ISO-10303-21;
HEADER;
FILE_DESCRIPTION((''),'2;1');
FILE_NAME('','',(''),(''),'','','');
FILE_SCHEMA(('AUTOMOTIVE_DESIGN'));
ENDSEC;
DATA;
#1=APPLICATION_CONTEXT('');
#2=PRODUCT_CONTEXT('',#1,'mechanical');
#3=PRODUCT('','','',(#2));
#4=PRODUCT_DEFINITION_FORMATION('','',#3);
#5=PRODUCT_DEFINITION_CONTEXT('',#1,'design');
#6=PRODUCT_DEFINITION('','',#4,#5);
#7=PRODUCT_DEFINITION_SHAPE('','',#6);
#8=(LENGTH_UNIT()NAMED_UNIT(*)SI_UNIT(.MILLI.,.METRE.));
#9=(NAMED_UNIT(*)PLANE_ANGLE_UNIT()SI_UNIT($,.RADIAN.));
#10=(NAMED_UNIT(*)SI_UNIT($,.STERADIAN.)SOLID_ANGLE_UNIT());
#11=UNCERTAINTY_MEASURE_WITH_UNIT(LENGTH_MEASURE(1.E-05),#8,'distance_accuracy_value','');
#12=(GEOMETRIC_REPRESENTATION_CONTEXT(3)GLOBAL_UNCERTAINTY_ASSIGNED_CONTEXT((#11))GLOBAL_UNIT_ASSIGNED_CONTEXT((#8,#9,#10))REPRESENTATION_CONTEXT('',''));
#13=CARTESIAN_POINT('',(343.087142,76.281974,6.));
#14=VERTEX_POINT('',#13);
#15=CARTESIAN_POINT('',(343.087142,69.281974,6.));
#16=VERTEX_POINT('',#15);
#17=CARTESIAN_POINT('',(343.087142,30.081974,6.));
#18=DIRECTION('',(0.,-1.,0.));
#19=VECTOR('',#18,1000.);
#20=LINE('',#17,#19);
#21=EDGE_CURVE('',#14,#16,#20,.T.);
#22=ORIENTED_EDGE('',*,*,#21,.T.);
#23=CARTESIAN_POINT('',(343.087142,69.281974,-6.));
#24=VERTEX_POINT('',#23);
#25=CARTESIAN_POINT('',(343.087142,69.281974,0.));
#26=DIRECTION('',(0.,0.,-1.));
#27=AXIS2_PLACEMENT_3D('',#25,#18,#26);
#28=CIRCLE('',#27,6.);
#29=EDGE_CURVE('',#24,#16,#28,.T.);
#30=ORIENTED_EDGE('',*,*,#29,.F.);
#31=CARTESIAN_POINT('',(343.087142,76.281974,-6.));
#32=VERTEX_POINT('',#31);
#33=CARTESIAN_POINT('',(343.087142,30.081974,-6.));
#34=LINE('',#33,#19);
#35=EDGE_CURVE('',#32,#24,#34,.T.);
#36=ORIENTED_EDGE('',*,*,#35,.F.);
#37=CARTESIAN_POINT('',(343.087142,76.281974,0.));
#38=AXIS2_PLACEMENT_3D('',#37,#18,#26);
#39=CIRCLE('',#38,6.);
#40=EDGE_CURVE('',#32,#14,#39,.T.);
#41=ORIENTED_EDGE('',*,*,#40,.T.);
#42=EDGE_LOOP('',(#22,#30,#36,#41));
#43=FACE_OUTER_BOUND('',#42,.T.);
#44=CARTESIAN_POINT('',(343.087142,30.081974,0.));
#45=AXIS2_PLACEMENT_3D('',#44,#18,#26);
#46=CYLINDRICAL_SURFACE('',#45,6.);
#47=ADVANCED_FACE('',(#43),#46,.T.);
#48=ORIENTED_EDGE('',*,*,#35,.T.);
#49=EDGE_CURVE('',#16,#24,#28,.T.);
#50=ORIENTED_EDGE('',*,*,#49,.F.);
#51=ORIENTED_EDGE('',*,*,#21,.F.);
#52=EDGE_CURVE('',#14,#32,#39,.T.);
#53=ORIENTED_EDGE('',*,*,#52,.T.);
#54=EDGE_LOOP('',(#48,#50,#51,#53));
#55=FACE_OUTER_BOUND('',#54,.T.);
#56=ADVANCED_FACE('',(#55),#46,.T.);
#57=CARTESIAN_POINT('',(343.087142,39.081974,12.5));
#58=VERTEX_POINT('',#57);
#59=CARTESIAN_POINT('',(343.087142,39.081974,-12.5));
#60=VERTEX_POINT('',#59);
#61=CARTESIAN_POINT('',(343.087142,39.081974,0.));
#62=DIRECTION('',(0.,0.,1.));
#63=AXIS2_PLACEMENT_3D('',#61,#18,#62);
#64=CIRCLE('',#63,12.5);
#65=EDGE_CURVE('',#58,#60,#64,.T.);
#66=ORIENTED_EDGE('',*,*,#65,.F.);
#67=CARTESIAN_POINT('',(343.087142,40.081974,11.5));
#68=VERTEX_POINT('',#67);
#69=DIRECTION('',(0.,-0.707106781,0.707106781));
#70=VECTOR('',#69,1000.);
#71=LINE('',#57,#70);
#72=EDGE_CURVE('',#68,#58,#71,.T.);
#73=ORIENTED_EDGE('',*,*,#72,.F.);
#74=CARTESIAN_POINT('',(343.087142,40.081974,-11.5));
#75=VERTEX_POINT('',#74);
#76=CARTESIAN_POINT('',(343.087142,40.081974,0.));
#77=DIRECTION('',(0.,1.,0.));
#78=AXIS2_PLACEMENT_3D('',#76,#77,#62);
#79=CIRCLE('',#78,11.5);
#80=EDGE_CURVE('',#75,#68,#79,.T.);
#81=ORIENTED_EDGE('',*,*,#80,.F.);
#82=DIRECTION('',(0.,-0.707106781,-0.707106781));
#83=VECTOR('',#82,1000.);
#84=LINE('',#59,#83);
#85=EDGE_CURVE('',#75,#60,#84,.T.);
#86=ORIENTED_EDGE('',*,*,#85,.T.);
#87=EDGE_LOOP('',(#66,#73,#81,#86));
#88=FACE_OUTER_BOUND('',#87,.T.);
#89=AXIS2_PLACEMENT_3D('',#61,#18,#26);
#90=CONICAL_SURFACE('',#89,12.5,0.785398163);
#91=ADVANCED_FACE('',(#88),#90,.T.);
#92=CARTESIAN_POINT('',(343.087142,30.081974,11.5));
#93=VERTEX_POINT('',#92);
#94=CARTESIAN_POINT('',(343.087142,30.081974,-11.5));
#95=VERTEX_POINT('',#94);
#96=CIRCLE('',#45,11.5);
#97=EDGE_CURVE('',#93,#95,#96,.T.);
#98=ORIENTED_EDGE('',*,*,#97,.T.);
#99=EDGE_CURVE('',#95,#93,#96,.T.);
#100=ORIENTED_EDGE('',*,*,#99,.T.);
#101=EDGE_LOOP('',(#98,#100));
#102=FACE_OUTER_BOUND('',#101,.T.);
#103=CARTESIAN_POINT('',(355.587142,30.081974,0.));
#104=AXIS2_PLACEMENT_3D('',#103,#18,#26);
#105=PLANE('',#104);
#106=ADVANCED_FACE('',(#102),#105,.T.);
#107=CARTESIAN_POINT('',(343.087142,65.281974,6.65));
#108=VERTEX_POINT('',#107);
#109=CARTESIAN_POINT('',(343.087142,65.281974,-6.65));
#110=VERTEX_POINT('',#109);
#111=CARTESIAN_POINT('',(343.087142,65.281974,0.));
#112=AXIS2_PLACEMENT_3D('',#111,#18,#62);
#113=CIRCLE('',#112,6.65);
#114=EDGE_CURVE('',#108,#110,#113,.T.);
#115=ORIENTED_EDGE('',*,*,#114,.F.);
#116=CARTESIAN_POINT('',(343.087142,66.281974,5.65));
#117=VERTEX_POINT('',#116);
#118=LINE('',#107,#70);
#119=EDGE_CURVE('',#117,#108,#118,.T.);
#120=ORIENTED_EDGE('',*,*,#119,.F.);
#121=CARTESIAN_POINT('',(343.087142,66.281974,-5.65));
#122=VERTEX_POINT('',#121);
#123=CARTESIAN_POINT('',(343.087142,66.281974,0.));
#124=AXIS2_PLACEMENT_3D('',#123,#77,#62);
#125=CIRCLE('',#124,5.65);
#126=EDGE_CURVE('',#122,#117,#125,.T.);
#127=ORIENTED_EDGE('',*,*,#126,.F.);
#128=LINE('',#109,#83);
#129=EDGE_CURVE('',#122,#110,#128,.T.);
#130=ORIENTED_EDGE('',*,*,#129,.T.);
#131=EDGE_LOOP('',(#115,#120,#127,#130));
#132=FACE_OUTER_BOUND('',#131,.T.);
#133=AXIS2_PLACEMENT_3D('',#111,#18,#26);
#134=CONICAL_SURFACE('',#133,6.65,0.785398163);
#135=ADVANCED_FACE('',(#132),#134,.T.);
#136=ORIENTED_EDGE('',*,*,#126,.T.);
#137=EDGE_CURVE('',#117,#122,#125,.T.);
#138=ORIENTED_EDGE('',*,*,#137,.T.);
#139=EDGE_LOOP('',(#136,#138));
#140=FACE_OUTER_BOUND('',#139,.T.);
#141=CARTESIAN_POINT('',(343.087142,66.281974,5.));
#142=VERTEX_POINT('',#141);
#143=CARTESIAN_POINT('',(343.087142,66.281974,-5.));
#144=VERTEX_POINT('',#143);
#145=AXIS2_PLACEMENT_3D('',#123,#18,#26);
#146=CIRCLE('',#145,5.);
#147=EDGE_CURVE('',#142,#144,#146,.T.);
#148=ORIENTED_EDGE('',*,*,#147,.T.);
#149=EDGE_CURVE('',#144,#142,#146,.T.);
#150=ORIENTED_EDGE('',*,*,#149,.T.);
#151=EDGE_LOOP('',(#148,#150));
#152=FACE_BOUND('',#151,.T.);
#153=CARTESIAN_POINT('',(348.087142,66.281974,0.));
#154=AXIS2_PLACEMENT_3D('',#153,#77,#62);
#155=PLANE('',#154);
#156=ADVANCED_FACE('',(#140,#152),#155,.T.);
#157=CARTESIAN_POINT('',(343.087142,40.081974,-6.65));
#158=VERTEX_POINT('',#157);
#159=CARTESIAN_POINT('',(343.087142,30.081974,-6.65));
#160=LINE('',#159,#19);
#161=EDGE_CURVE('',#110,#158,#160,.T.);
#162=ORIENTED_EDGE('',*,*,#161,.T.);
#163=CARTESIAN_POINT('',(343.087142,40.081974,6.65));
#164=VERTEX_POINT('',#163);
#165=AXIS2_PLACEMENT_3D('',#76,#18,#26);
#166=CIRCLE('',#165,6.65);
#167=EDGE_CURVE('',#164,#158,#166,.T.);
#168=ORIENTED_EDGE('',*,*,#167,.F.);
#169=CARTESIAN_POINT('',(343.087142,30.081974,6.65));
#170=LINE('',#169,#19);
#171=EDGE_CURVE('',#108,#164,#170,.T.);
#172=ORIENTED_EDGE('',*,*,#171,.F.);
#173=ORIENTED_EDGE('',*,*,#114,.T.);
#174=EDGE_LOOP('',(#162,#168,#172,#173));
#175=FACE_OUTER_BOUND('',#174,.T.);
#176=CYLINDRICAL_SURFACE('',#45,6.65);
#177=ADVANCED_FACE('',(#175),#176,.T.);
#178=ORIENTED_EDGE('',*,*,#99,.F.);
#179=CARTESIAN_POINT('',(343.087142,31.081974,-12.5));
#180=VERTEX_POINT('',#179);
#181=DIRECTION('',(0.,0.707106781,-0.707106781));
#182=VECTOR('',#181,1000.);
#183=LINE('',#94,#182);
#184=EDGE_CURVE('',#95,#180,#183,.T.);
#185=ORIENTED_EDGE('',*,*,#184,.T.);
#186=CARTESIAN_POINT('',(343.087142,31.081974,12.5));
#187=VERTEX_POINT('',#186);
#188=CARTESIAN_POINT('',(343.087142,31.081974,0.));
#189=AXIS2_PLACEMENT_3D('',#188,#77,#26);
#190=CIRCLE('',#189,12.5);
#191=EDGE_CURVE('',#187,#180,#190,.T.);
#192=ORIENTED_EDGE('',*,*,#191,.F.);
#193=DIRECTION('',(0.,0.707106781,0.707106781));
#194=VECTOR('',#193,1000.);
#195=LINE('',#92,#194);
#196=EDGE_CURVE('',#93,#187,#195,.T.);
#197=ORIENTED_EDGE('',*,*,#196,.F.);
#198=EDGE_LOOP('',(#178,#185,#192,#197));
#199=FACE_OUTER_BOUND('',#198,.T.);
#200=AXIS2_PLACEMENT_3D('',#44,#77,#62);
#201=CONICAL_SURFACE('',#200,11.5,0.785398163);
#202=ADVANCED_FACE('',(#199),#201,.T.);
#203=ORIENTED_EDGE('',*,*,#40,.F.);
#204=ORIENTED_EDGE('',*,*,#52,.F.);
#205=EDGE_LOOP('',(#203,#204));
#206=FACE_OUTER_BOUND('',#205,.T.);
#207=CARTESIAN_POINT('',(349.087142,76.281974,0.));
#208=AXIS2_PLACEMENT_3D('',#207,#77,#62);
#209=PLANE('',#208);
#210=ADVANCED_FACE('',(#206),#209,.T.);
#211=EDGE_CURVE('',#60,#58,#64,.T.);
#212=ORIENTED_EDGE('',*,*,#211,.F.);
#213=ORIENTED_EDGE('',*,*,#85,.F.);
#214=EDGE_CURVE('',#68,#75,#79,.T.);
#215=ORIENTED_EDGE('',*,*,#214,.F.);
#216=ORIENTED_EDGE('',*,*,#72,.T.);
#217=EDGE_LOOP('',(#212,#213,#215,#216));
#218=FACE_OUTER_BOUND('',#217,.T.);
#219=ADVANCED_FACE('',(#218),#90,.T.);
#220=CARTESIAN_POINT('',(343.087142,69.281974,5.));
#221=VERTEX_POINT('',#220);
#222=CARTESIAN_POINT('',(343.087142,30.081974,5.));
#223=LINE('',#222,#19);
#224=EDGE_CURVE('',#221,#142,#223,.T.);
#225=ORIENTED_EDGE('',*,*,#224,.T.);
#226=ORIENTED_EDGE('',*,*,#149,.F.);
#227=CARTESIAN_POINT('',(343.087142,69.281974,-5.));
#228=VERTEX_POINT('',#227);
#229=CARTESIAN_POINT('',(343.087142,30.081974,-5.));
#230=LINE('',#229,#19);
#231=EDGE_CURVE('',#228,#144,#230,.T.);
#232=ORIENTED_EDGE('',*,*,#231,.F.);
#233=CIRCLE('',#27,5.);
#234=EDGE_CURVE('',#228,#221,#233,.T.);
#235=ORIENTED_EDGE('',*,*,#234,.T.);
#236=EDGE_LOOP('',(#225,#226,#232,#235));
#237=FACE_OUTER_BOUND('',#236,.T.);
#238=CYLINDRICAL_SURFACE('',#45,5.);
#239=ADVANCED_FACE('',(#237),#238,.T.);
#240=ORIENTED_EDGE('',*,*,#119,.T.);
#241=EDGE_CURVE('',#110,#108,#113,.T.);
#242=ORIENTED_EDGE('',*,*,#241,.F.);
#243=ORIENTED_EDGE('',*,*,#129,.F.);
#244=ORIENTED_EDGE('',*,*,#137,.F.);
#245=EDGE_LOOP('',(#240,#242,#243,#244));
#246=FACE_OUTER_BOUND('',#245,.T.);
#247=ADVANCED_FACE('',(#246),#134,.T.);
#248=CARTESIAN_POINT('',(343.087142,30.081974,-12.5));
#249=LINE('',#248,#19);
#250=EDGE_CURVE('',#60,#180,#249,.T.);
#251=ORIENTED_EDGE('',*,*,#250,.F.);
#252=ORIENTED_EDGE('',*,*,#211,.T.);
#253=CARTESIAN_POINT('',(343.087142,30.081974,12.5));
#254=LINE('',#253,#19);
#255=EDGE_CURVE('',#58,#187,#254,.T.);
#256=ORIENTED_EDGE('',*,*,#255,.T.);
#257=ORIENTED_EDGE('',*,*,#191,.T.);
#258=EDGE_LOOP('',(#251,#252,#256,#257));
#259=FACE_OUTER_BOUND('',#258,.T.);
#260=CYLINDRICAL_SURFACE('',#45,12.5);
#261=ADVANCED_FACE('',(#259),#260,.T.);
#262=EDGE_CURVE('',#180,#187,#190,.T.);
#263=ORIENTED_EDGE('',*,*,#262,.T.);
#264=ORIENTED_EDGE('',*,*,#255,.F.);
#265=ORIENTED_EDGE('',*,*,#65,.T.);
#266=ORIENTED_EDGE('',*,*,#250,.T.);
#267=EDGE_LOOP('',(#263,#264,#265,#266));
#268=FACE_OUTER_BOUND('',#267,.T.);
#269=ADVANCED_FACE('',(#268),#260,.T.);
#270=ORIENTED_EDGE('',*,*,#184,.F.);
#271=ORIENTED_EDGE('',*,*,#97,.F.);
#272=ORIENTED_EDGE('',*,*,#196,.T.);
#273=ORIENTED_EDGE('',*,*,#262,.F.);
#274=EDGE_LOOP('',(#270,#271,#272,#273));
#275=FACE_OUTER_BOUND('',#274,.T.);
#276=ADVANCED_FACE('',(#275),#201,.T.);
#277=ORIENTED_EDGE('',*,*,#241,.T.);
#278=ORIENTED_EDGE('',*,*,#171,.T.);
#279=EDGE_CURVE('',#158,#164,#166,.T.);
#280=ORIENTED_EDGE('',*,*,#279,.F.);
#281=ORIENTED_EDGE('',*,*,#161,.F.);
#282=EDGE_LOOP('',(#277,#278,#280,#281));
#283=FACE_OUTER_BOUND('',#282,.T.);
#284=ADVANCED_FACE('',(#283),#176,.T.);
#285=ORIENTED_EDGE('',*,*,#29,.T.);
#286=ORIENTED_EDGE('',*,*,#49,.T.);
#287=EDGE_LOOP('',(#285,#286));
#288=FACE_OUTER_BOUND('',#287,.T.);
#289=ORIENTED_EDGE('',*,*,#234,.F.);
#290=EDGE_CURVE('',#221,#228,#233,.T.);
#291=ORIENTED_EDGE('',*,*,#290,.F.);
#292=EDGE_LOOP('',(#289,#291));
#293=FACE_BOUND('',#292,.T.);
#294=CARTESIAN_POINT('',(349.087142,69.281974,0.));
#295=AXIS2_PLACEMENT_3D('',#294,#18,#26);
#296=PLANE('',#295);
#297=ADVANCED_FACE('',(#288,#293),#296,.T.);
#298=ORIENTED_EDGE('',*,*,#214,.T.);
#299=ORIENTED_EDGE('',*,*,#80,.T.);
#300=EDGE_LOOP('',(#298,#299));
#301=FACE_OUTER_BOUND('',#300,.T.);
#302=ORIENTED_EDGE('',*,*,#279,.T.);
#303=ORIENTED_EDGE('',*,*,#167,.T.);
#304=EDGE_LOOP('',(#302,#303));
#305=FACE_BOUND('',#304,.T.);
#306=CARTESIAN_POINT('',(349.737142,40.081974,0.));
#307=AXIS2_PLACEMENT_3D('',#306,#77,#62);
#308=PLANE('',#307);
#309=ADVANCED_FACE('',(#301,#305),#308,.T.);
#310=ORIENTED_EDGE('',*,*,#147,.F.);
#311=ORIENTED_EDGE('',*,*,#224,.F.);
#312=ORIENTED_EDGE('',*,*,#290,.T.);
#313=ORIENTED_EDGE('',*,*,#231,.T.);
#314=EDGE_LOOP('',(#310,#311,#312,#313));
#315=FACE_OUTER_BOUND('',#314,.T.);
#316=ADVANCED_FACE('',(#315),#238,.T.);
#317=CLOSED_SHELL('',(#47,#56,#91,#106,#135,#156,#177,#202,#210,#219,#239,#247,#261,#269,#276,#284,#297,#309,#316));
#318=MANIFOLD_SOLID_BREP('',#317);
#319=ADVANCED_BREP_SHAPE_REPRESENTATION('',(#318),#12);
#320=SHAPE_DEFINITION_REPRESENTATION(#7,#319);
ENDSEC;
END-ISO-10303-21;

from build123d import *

# Parameters (mm, degrees)
CHAMFER_1_SIZE = 1


with BuildPart() as part:
    # 草图1 → 旋转1 (revolve)
    with BuildSketch(Plane.XY, mode=Mode.PRIVATE) as revolve_1_sk:
        Polygon((349.087142185, 76.281973739), (349.087142185, 69.281973739), (348.087142185, 69.281973739), (348.087142185, 66.281973739), (349.737142185, 66.281973739), (349.737142185, 40.081973739), (355.587142185, 40.081973739), (355.587142185, 30.081973739), (343.087142185, 30.081973739), (343.087142185, 76.281973739), align=None)
    revolve(revolve_1_sk.sketch.rotate(Axis((343.087142185, 30.081973739, 0), (0, 1, 0)), 90), axis=Axis((343.087142185, 30.081973739, 0), (0, 1, 0)))

    # 倒角1
    chamfer_1_edges = [part.edges().sort_by_distance(p)[0] for p in [
        (343.087142185, 66.281973739, 6.65),
        (343.087142185, 30.081973739, 12.5),
        (343.087142185, 40.081973739, 12.5),
    ]]
    chamfer(chamfer_1_edges, length=CHAMFER_1_SIZE)


solid = part.part
